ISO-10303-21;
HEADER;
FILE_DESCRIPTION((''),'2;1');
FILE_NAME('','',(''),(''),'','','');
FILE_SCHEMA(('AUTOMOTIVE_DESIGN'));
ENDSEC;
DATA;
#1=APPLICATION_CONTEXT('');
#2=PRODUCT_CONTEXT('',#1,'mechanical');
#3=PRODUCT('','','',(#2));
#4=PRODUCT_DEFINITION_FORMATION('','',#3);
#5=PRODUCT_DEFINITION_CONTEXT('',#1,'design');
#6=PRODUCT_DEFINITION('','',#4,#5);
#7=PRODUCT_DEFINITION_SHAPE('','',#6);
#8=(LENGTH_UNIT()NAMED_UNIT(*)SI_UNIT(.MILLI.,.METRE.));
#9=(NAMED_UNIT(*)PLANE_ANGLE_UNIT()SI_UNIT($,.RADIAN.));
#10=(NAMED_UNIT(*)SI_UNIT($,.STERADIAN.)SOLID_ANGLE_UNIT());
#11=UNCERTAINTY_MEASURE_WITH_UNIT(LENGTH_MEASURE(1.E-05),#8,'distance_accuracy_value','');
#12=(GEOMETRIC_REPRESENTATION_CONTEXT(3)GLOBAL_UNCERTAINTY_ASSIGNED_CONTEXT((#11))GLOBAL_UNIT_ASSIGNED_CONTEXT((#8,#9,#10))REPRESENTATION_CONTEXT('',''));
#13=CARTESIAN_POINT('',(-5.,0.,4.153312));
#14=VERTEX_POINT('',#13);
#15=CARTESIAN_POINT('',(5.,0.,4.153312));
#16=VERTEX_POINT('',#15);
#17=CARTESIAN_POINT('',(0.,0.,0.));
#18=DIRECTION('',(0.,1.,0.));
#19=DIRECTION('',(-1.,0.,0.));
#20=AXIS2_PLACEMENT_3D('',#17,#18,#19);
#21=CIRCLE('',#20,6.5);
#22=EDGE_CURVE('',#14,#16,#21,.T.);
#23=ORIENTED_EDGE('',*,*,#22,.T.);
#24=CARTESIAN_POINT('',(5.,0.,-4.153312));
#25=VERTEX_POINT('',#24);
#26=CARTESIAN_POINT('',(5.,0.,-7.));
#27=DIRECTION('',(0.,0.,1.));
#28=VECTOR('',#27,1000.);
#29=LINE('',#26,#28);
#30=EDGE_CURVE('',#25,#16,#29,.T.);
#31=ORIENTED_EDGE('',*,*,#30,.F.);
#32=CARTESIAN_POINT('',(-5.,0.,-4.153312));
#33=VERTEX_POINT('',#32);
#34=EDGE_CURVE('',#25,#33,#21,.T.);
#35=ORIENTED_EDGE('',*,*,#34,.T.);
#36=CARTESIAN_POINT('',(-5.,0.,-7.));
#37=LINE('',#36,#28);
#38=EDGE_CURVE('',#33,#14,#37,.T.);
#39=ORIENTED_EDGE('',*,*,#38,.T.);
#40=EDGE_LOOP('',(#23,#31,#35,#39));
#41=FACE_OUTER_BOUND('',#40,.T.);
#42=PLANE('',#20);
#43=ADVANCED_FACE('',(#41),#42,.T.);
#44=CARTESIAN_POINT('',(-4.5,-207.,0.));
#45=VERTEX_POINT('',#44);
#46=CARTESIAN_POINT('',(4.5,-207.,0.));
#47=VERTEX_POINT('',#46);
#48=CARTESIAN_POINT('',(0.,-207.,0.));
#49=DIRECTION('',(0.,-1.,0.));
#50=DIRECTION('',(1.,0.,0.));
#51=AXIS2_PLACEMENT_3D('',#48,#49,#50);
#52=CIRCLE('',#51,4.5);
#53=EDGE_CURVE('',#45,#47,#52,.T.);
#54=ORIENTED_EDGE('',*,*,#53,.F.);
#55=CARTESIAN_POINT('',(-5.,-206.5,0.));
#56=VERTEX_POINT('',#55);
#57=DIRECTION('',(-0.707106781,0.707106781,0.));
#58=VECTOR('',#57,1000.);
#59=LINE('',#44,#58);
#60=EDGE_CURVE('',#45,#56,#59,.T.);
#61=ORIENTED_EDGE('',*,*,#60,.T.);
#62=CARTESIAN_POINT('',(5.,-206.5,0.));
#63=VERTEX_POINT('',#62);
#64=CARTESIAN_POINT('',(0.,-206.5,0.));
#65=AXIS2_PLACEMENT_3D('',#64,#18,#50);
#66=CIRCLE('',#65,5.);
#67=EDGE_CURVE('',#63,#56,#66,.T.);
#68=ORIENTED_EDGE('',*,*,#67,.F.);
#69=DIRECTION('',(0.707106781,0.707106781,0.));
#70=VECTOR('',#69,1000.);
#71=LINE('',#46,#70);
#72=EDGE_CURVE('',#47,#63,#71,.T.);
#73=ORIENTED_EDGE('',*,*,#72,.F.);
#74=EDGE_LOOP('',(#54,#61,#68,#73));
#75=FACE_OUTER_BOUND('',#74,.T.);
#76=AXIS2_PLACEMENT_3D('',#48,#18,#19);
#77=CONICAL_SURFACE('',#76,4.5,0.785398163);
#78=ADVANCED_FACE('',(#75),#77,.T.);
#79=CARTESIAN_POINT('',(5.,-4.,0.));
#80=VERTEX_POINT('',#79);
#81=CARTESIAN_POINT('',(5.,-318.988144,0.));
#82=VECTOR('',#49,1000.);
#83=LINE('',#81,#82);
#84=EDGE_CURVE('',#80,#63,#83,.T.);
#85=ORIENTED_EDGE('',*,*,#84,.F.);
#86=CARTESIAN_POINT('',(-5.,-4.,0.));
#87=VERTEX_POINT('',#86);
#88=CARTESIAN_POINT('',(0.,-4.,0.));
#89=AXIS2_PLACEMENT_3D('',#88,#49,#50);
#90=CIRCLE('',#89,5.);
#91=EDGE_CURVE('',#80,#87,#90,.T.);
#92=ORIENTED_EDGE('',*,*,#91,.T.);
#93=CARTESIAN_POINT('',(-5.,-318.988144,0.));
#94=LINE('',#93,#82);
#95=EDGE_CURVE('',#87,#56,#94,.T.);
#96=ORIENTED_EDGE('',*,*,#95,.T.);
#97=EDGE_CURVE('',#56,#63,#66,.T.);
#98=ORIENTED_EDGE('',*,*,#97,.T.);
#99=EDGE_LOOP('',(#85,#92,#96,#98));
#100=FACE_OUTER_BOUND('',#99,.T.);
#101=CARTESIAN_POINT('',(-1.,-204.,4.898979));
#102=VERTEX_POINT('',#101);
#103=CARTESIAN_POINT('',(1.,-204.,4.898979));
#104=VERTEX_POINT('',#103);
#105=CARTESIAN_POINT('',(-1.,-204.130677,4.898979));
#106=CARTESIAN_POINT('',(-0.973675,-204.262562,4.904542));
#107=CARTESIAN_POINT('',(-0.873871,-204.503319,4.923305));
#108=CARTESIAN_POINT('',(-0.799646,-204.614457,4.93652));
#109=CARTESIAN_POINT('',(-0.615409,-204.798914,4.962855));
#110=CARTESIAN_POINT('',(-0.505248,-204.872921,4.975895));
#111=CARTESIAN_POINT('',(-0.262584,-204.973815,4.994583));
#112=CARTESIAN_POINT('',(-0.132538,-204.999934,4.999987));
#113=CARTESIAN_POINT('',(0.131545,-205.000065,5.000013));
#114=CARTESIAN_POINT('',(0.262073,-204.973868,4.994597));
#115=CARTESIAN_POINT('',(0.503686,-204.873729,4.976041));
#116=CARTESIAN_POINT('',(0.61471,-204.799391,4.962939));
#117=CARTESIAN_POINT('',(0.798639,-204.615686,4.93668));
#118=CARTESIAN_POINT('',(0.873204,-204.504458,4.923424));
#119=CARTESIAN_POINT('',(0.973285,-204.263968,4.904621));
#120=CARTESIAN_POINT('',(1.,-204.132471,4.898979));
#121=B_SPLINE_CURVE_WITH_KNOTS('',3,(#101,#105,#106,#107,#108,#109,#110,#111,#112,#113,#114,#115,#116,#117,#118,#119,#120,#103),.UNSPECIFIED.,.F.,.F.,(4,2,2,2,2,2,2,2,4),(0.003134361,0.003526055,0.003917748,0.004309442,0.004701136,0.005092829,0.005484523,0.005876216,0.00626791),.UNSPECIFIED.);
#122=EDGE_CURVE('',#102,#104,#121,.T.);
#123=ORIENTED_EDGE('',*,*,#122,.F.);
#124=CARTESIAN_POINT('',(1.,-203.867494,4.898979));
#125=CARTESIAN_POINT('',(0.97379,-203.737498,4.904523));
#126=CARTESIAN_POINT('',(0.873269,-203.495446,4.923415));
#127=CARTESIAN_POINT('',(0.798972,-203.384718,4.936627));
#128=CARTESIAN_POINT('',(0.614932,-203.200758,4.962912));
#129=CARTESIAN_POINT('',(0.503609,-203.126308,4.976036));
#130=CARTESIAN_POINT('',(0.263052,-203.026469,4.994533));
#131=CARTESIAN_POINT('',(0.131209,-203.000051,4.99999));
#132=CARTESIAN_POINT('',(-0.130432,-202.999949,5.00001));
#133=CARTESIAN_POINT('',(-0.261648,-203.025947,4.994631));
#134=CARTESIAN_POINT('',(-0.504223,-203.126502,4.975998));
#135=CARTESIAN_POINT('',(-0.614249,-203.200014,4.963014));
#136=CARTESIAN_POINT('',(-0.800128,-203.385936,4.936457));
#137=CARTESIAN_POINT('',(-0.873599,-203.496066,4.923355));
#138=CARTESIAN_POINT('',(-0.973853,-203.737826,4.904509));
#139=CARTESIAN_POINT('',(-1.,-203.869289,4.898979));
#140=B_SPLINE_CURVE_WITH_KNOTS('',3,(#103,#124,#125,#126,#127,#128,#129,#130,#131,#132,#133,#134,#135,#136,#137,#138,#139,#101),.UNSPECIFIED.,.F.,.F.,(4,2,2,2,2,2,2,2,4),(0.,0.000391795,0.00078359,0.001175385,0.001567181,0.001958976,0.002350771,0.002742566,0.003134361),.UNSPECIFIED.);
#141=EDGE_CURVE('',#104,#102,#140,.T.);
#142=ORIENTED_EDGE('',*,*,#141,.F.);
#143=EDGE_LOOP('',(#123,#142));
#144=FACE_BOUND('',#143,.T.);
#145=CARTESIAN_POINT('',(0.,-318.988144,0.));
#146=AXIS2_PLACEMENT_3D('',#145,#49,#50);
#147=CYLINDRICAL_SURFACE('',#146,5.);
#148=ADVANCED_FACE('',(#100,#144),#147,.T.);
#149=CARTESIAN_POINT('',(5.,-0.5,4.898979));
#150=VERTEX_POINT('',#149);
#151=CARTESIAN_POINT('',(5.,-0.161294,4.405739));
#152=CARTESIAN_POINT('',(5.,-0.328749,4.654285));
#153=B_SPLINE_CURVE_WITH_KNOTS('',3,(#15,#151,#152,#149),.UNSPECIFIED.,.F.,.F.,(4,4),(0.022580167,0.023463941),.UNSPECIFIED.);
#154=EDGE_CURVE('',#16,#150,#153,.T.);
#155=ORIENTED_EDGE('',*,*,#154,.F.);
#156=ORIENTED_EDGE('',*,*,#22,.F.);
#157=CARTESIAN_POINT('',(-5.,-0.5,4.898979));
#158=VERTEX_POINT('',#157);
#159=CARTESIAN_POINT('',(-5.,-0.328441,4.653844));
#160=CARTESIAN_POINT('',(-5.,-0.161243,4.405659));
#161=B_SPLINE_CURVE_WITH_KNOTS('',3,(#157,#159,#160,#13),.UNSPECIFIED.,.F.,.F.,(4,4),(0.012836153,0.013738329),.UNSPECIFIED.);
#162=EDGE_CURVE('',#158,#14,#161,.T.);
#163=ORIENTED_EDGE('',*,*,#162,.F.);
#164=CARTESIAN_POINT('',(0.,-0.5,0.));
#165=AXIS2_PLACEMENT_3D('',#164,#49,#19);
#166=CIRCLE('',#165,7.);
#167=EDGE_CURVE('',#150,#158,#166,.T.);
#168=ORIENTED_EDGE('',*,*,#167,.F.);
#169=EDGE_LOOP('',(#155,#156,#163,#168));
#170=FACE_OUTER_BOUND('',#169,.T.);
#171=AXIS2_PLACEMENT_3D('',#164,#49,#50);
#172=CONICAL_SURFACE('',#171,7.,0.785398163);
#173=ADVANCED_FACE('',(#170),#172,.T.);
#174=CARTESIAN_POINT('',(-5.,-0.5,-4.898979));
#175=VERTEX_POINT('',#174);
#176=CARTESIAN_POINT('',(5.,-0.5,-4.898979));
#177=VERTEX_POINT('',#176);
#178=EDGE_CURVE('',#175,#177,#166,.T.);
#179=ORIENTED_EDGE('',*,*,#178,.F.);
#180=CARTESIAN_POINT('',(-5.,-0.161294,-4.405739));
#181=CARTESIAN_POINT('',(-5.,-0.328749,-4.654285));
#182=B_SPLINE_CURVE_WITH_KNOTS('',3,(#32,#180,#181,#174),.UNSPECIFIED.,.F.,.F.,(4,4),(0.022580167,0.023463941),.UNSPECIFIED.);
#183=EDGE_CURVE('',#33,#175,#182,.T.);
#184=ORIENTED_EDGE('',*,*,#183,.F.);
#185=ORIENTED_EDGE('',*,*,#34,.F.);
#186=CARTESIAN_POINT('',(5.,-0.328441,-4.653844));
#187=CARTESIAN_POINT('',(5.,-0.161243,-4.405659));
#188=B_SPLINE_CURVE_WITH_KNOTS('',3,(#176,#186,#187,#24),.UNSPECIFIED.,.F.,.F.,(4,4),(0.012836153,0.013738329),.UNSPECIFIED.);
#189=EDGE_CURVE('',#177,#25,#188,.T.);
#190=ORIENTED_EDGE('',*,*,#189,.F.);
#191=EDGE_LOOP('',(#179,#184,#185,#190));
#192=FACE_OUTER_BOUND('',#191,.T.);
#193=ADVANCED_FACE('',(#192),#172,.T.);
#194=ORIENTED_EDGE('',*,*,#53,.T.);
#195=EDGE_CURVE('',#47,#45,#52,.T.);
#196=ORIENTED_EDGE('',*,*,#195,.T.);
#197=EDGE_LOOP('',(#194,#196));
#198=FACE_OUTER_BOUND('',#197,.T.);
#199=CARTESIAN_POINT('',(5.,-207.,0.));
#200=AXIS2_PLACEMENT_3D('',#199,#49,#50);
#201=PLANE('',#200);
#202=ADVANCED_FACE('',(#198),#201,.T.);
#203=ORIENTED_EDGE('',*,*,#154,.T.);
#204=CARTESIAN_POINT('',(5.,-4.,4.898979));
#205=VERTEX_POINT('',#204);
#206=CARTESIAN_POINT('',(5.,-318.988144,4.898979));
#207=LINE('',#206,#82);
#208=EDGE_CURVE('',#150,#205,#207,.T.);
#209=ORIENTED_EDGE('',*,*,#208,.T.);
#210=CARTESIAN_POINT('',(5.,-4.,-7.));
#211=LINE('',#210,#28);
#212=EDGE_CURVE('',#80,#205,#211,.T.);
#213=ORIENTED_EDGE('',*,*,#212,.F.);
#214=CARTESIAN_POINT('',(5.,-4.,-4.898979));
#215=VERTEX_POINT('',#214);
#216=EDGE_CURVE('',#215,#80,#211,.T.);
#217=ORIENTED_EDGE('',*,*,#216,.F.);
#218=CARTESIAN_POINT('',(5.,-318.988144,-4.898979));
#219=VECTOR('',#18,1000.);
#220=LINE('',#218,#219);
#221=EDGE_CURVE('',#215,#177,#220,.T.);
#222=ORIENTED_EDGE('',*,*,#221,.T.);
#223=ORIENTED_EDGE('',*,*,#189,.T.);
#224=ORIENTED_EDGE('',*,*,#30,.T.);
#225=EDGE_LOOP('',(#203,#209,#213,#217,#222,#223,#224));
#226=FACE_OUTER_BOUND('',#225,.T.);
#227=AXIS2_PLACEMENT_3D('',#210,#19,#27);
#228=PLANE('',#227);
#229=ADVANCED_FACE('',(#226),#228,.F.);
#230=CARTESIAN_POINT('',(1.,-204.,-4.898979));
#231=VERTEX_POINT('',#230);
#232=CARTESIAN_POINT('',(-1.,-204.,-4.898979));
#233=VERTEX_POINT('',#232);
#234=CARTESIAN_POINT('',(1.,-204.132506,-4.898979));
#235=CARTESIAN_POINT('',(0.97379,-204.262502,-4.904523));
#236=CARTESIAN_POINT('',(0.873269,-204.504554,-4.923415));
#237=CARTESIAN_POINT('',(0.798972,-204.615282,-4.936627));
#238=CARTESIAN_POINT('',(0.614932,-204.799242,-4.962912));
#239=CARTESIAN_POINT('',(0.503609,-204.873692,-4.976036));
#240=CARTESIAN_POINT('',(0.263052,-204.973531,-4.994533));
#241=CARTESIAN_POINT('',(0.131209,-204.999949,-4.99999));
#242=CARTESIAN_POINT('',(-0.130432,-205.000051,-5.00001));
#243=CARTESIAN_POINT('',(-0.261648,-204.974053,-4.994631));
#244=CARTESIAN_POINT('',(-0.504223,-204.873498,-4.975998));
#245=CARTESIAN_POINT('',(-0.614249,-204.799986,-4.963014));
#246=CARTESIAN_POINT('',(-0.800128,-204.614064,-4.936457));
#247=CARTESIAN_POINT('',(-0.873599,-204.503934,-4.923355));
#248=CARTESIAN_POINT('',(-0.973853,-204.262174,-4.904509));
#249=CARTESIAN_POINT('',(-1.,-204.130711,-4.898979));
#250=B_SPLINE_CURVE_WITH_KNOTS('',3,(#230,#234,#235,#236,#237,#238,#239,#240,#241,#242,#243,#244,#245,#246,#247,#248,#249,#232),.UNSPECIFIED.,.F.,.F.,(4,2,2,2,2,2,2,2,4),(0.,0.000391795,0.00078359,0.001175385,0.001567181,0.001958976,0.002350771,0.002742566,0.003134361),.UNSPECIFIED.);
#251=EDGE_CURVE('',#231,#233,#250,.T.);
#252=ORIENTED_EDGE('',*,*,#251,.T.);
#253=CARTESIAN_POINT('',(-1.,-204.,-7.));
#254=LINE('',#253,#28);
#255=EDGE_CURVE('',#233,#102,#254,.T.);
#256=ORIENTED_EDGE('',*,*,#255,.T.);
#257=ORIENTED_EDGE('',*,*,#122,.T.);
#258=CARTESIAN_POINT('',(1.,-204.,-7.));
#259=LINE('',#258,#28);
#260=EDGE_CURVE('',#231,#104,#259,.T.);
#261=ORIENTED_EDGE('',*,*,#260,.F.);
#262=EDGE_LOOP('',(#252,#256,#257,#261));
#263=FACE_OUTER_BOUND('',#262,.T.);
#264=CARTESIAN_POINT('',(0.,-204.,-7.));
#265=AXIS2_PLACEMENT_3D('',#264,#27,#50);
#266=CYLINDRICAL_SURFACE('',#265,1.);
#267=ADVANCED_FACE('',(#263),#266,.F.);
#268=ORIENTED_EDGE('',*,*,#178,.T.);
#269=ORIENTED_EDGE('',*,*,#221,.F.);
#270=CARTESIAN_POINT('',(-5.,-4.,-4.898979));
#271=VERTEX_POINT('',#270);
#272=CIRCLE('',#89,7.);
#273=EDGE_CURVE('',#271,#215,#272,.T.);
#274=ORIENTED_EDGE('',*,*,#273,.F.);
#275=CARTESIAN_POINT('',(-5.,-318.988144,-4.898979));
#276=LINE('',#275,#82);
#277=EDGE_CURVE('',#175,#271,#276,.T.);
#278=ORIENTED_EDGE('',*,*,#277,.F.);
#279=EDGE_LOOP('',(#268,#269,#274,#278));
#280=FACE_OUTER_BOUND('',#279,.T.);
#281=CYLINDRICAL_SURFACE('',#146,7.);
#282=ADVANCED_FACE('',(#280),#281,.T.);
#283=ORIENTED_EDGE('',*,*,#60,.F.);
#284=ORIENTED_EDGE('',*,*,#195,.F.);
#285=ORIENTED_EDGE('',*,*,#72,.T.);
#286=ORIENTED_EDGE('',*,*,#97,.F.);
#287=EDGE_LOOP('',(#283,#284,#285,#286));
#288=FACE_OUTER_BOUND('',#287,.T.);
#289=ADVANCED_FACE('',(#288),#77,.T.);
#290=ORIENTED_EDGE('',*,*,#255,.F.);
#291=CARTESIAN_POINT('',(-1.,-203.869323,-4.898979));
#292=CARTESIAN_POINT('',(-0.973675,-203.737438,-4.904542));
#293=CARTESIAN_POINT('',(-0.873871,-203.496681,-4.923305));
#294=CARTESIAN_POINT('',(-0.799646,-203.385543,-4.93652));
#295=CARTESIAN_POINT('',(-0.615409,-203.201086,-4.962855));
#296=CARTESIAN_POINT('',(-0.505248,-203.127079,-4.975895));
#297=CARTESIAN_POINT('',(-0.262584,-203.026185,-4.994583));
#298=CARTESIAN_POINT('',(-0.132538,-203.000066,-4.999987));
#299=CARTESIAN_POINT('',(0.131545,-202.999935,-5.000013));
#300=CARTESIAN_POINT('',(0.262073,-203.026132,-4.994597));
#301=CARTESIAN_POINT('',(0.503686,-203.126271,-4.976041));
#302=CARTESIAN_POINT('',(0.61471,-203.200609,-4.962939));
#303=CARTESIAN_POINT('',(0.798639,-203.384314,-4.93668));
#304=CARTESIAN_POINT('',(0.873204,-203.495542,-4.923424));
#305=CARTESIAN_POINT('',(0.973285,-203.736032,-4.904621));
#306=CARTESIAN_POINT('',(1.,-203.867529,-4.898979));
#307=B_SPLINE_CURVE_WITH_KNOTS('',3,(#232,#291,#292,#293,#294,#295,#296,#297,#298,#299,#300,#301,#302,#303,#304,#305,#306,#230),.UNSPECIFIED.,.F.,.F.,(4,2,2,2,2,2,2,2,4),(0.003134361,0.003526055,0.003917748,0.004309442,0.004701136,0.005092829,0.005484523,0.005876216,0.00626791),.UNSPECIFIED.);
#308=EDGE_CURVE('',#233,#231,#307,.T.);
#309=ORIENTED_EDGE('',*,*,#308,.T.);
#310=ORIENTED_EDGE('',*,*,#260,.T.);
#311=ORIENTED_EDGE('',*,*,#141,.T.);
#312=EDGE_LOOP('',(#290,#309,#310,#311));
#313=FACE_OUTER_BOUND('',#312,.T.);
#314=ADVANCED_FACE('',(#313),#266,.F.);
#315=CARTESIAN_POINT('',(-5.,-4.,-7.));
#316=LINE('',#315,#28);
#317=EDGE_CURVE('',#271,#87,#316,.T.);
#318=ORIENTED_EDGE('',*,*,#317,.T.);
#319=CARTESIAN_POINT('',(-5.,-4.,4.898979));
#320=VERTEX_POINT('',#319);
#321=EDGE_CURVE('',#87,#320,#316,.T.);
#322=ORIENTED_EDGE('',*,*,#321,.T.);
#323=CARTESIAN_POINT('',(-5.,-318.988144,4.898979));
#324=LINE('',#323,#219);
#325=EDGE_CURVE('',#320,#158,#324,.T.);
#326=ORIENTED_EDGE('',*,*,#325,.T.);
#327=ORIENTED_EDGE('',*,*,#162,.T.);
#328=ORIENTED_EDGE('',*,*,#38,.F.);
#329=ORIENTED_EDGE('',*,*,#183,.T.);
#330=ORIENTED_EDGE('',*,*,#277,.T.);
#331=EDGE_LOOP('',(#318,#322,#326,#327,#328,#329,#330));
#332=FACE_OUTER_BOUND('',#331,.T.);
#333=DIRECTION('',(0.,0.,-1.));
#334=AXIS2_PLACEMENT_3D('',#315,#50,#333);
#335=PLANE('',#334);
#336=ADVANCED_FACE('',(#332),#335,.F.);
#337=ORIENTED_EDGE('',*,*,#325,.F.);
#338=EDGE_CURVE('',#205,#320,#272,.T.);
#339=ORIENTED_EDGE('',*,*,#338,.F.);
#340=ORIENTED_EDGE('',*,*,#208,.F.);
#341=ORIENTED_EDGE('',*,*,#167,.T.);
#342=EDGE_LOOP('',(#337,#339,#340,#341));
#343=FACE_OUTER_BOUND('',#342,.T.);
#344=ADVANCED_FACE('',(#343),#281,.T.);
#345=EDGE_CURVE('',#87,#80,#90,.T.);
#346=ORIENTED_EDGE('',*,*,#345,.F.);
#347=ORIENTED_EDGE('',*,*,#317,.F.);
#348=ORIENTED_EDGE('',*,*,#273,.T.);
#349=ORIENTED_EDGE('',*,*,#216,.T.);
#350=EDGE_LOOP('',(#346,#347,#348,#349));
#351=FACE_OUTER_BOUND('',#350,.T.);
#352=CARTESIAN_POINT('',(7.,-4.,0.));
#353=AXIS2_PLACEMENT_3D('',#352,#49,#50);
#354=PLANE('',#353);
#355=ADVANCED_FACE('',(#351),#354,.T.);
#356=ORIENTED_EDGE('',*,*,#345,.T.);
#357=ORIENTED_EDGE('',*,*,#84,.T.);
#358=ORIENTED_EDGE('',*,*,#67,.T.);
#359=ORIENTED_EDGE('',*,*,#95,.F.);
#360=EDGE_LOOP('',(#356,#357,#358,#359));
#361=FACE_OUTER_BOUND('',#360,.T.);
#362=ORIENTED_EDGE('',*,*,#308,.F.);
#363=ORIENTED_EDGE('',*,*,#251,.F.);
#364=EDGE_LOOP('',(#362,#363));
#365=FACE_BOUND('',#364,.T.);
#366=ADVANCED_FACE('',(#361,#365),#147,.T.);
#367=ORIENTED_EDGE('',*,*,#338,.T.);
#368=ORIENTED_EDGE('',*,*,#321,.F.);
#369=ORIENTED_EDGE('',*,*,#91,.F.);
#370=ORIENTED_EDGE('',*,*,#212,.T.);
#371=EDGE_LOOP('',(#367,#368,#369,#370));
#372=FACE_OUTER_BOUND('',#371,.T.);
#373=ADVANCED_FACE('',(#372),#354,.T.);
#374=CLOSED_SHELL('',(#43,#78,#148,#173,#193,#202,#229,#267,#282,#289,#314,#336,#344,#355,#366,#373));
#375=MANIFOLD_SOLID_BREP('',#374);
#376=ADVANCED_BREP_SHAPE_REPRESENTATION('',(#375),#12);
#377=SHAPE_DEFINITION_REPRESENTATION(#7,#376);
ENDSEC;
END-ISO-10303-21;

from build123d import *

# Parameters (mm, degrees)
CHAMFER1_SIZE           = 0.5
CUT_EXTRUDE1_DEPTH      = 208.236579783
CUT_EXTRUDE1_DEPTH_BACK = 208.236579783
SKETCH2_R               = 1
CUT_EXTRUDE2_DEPTH      = 208.236579783
CUT_EXTRUDE2_DEPTH_BACK = 208.236579783
SKETCH3_W               = 2
SKETCH3_H               = 4
CUT_EXTRUDE3_DEPTH      = 208.236579783
CUT_EXTRUDE3_DEPTH_BACK = 208.236579783
SKETCH4_W               = 2
SKETCH4_H               = 4


with BuildPart() as part:
    # Sketch1 → Revolve1 (revolve)
    with BuildSketch(Plane.XY):
        Polygon((0, 0), (7, 0), (7, -4), (5, -4), (5, -207), (0, -207), align=None)
    revolve(axis=Axis((0, -318.988143723, 0), (0, 1, 0)))

    # Chamfer1
    chamfer1_edges = [part.edges().sort_by_distance(p)[0] for p in [
        (-5, -207, 0),
        (-7, 0, 0),
    ]]
    chamfer(chamfer1_edges, length=CHAMFER1_SIZE)

    # Sketch2 → Cut-Extrude1 (cut, two sides: drawn at the far end of the back side and taken through both)
    with BuildSketch(Plane.XY.offset(-CUT_EXTRUDE1_DEPTH_BACK)):
        with Locations((0, -204)):
            Circle(SKETCH2_R)
    extrude(amount=CUT_EXTRUDE1_DEPTH + CUT_EXTRUDE1_DEPTH_BACK, mode=Mode.SUBTRACT)

    # Sketch3 → Cut-Extrude2 (cut, two sides: drawn at the far end of the back side and taken through both)
    with BuildSketch(Plane.XY.offset(-CUT_EXTRUDE2_DEPTH_BACK)):
        with Locations((-6, -2)):
            Rectangle(SKETCH3_W, SKETCH3_H)
    extrude(amount=CUT_EXTRUDE2_DEPTH + CUT_EXTRUDE2_DEPTH_BACK, mode=Mode.SUBTRACT)

    # Sketch4 → Cut-Extrude3 (cut, two sides: drawn at the far end of the back side and taken through both)
    with BuildSketch(Plane.XY.offset(-CUT_EXTRUDE3_DEPTH_BACK)):
        with Locations((6, -2)):
            Rectangle(SKETCH4_W, SKETCH4_H)
    extrude(amount=CUT_EXTRUDE3_DEPTH + CUT_EXTRUDE3_DEPTH_BACK, mode=Mode.SUBTRACT)


solid = part.part
